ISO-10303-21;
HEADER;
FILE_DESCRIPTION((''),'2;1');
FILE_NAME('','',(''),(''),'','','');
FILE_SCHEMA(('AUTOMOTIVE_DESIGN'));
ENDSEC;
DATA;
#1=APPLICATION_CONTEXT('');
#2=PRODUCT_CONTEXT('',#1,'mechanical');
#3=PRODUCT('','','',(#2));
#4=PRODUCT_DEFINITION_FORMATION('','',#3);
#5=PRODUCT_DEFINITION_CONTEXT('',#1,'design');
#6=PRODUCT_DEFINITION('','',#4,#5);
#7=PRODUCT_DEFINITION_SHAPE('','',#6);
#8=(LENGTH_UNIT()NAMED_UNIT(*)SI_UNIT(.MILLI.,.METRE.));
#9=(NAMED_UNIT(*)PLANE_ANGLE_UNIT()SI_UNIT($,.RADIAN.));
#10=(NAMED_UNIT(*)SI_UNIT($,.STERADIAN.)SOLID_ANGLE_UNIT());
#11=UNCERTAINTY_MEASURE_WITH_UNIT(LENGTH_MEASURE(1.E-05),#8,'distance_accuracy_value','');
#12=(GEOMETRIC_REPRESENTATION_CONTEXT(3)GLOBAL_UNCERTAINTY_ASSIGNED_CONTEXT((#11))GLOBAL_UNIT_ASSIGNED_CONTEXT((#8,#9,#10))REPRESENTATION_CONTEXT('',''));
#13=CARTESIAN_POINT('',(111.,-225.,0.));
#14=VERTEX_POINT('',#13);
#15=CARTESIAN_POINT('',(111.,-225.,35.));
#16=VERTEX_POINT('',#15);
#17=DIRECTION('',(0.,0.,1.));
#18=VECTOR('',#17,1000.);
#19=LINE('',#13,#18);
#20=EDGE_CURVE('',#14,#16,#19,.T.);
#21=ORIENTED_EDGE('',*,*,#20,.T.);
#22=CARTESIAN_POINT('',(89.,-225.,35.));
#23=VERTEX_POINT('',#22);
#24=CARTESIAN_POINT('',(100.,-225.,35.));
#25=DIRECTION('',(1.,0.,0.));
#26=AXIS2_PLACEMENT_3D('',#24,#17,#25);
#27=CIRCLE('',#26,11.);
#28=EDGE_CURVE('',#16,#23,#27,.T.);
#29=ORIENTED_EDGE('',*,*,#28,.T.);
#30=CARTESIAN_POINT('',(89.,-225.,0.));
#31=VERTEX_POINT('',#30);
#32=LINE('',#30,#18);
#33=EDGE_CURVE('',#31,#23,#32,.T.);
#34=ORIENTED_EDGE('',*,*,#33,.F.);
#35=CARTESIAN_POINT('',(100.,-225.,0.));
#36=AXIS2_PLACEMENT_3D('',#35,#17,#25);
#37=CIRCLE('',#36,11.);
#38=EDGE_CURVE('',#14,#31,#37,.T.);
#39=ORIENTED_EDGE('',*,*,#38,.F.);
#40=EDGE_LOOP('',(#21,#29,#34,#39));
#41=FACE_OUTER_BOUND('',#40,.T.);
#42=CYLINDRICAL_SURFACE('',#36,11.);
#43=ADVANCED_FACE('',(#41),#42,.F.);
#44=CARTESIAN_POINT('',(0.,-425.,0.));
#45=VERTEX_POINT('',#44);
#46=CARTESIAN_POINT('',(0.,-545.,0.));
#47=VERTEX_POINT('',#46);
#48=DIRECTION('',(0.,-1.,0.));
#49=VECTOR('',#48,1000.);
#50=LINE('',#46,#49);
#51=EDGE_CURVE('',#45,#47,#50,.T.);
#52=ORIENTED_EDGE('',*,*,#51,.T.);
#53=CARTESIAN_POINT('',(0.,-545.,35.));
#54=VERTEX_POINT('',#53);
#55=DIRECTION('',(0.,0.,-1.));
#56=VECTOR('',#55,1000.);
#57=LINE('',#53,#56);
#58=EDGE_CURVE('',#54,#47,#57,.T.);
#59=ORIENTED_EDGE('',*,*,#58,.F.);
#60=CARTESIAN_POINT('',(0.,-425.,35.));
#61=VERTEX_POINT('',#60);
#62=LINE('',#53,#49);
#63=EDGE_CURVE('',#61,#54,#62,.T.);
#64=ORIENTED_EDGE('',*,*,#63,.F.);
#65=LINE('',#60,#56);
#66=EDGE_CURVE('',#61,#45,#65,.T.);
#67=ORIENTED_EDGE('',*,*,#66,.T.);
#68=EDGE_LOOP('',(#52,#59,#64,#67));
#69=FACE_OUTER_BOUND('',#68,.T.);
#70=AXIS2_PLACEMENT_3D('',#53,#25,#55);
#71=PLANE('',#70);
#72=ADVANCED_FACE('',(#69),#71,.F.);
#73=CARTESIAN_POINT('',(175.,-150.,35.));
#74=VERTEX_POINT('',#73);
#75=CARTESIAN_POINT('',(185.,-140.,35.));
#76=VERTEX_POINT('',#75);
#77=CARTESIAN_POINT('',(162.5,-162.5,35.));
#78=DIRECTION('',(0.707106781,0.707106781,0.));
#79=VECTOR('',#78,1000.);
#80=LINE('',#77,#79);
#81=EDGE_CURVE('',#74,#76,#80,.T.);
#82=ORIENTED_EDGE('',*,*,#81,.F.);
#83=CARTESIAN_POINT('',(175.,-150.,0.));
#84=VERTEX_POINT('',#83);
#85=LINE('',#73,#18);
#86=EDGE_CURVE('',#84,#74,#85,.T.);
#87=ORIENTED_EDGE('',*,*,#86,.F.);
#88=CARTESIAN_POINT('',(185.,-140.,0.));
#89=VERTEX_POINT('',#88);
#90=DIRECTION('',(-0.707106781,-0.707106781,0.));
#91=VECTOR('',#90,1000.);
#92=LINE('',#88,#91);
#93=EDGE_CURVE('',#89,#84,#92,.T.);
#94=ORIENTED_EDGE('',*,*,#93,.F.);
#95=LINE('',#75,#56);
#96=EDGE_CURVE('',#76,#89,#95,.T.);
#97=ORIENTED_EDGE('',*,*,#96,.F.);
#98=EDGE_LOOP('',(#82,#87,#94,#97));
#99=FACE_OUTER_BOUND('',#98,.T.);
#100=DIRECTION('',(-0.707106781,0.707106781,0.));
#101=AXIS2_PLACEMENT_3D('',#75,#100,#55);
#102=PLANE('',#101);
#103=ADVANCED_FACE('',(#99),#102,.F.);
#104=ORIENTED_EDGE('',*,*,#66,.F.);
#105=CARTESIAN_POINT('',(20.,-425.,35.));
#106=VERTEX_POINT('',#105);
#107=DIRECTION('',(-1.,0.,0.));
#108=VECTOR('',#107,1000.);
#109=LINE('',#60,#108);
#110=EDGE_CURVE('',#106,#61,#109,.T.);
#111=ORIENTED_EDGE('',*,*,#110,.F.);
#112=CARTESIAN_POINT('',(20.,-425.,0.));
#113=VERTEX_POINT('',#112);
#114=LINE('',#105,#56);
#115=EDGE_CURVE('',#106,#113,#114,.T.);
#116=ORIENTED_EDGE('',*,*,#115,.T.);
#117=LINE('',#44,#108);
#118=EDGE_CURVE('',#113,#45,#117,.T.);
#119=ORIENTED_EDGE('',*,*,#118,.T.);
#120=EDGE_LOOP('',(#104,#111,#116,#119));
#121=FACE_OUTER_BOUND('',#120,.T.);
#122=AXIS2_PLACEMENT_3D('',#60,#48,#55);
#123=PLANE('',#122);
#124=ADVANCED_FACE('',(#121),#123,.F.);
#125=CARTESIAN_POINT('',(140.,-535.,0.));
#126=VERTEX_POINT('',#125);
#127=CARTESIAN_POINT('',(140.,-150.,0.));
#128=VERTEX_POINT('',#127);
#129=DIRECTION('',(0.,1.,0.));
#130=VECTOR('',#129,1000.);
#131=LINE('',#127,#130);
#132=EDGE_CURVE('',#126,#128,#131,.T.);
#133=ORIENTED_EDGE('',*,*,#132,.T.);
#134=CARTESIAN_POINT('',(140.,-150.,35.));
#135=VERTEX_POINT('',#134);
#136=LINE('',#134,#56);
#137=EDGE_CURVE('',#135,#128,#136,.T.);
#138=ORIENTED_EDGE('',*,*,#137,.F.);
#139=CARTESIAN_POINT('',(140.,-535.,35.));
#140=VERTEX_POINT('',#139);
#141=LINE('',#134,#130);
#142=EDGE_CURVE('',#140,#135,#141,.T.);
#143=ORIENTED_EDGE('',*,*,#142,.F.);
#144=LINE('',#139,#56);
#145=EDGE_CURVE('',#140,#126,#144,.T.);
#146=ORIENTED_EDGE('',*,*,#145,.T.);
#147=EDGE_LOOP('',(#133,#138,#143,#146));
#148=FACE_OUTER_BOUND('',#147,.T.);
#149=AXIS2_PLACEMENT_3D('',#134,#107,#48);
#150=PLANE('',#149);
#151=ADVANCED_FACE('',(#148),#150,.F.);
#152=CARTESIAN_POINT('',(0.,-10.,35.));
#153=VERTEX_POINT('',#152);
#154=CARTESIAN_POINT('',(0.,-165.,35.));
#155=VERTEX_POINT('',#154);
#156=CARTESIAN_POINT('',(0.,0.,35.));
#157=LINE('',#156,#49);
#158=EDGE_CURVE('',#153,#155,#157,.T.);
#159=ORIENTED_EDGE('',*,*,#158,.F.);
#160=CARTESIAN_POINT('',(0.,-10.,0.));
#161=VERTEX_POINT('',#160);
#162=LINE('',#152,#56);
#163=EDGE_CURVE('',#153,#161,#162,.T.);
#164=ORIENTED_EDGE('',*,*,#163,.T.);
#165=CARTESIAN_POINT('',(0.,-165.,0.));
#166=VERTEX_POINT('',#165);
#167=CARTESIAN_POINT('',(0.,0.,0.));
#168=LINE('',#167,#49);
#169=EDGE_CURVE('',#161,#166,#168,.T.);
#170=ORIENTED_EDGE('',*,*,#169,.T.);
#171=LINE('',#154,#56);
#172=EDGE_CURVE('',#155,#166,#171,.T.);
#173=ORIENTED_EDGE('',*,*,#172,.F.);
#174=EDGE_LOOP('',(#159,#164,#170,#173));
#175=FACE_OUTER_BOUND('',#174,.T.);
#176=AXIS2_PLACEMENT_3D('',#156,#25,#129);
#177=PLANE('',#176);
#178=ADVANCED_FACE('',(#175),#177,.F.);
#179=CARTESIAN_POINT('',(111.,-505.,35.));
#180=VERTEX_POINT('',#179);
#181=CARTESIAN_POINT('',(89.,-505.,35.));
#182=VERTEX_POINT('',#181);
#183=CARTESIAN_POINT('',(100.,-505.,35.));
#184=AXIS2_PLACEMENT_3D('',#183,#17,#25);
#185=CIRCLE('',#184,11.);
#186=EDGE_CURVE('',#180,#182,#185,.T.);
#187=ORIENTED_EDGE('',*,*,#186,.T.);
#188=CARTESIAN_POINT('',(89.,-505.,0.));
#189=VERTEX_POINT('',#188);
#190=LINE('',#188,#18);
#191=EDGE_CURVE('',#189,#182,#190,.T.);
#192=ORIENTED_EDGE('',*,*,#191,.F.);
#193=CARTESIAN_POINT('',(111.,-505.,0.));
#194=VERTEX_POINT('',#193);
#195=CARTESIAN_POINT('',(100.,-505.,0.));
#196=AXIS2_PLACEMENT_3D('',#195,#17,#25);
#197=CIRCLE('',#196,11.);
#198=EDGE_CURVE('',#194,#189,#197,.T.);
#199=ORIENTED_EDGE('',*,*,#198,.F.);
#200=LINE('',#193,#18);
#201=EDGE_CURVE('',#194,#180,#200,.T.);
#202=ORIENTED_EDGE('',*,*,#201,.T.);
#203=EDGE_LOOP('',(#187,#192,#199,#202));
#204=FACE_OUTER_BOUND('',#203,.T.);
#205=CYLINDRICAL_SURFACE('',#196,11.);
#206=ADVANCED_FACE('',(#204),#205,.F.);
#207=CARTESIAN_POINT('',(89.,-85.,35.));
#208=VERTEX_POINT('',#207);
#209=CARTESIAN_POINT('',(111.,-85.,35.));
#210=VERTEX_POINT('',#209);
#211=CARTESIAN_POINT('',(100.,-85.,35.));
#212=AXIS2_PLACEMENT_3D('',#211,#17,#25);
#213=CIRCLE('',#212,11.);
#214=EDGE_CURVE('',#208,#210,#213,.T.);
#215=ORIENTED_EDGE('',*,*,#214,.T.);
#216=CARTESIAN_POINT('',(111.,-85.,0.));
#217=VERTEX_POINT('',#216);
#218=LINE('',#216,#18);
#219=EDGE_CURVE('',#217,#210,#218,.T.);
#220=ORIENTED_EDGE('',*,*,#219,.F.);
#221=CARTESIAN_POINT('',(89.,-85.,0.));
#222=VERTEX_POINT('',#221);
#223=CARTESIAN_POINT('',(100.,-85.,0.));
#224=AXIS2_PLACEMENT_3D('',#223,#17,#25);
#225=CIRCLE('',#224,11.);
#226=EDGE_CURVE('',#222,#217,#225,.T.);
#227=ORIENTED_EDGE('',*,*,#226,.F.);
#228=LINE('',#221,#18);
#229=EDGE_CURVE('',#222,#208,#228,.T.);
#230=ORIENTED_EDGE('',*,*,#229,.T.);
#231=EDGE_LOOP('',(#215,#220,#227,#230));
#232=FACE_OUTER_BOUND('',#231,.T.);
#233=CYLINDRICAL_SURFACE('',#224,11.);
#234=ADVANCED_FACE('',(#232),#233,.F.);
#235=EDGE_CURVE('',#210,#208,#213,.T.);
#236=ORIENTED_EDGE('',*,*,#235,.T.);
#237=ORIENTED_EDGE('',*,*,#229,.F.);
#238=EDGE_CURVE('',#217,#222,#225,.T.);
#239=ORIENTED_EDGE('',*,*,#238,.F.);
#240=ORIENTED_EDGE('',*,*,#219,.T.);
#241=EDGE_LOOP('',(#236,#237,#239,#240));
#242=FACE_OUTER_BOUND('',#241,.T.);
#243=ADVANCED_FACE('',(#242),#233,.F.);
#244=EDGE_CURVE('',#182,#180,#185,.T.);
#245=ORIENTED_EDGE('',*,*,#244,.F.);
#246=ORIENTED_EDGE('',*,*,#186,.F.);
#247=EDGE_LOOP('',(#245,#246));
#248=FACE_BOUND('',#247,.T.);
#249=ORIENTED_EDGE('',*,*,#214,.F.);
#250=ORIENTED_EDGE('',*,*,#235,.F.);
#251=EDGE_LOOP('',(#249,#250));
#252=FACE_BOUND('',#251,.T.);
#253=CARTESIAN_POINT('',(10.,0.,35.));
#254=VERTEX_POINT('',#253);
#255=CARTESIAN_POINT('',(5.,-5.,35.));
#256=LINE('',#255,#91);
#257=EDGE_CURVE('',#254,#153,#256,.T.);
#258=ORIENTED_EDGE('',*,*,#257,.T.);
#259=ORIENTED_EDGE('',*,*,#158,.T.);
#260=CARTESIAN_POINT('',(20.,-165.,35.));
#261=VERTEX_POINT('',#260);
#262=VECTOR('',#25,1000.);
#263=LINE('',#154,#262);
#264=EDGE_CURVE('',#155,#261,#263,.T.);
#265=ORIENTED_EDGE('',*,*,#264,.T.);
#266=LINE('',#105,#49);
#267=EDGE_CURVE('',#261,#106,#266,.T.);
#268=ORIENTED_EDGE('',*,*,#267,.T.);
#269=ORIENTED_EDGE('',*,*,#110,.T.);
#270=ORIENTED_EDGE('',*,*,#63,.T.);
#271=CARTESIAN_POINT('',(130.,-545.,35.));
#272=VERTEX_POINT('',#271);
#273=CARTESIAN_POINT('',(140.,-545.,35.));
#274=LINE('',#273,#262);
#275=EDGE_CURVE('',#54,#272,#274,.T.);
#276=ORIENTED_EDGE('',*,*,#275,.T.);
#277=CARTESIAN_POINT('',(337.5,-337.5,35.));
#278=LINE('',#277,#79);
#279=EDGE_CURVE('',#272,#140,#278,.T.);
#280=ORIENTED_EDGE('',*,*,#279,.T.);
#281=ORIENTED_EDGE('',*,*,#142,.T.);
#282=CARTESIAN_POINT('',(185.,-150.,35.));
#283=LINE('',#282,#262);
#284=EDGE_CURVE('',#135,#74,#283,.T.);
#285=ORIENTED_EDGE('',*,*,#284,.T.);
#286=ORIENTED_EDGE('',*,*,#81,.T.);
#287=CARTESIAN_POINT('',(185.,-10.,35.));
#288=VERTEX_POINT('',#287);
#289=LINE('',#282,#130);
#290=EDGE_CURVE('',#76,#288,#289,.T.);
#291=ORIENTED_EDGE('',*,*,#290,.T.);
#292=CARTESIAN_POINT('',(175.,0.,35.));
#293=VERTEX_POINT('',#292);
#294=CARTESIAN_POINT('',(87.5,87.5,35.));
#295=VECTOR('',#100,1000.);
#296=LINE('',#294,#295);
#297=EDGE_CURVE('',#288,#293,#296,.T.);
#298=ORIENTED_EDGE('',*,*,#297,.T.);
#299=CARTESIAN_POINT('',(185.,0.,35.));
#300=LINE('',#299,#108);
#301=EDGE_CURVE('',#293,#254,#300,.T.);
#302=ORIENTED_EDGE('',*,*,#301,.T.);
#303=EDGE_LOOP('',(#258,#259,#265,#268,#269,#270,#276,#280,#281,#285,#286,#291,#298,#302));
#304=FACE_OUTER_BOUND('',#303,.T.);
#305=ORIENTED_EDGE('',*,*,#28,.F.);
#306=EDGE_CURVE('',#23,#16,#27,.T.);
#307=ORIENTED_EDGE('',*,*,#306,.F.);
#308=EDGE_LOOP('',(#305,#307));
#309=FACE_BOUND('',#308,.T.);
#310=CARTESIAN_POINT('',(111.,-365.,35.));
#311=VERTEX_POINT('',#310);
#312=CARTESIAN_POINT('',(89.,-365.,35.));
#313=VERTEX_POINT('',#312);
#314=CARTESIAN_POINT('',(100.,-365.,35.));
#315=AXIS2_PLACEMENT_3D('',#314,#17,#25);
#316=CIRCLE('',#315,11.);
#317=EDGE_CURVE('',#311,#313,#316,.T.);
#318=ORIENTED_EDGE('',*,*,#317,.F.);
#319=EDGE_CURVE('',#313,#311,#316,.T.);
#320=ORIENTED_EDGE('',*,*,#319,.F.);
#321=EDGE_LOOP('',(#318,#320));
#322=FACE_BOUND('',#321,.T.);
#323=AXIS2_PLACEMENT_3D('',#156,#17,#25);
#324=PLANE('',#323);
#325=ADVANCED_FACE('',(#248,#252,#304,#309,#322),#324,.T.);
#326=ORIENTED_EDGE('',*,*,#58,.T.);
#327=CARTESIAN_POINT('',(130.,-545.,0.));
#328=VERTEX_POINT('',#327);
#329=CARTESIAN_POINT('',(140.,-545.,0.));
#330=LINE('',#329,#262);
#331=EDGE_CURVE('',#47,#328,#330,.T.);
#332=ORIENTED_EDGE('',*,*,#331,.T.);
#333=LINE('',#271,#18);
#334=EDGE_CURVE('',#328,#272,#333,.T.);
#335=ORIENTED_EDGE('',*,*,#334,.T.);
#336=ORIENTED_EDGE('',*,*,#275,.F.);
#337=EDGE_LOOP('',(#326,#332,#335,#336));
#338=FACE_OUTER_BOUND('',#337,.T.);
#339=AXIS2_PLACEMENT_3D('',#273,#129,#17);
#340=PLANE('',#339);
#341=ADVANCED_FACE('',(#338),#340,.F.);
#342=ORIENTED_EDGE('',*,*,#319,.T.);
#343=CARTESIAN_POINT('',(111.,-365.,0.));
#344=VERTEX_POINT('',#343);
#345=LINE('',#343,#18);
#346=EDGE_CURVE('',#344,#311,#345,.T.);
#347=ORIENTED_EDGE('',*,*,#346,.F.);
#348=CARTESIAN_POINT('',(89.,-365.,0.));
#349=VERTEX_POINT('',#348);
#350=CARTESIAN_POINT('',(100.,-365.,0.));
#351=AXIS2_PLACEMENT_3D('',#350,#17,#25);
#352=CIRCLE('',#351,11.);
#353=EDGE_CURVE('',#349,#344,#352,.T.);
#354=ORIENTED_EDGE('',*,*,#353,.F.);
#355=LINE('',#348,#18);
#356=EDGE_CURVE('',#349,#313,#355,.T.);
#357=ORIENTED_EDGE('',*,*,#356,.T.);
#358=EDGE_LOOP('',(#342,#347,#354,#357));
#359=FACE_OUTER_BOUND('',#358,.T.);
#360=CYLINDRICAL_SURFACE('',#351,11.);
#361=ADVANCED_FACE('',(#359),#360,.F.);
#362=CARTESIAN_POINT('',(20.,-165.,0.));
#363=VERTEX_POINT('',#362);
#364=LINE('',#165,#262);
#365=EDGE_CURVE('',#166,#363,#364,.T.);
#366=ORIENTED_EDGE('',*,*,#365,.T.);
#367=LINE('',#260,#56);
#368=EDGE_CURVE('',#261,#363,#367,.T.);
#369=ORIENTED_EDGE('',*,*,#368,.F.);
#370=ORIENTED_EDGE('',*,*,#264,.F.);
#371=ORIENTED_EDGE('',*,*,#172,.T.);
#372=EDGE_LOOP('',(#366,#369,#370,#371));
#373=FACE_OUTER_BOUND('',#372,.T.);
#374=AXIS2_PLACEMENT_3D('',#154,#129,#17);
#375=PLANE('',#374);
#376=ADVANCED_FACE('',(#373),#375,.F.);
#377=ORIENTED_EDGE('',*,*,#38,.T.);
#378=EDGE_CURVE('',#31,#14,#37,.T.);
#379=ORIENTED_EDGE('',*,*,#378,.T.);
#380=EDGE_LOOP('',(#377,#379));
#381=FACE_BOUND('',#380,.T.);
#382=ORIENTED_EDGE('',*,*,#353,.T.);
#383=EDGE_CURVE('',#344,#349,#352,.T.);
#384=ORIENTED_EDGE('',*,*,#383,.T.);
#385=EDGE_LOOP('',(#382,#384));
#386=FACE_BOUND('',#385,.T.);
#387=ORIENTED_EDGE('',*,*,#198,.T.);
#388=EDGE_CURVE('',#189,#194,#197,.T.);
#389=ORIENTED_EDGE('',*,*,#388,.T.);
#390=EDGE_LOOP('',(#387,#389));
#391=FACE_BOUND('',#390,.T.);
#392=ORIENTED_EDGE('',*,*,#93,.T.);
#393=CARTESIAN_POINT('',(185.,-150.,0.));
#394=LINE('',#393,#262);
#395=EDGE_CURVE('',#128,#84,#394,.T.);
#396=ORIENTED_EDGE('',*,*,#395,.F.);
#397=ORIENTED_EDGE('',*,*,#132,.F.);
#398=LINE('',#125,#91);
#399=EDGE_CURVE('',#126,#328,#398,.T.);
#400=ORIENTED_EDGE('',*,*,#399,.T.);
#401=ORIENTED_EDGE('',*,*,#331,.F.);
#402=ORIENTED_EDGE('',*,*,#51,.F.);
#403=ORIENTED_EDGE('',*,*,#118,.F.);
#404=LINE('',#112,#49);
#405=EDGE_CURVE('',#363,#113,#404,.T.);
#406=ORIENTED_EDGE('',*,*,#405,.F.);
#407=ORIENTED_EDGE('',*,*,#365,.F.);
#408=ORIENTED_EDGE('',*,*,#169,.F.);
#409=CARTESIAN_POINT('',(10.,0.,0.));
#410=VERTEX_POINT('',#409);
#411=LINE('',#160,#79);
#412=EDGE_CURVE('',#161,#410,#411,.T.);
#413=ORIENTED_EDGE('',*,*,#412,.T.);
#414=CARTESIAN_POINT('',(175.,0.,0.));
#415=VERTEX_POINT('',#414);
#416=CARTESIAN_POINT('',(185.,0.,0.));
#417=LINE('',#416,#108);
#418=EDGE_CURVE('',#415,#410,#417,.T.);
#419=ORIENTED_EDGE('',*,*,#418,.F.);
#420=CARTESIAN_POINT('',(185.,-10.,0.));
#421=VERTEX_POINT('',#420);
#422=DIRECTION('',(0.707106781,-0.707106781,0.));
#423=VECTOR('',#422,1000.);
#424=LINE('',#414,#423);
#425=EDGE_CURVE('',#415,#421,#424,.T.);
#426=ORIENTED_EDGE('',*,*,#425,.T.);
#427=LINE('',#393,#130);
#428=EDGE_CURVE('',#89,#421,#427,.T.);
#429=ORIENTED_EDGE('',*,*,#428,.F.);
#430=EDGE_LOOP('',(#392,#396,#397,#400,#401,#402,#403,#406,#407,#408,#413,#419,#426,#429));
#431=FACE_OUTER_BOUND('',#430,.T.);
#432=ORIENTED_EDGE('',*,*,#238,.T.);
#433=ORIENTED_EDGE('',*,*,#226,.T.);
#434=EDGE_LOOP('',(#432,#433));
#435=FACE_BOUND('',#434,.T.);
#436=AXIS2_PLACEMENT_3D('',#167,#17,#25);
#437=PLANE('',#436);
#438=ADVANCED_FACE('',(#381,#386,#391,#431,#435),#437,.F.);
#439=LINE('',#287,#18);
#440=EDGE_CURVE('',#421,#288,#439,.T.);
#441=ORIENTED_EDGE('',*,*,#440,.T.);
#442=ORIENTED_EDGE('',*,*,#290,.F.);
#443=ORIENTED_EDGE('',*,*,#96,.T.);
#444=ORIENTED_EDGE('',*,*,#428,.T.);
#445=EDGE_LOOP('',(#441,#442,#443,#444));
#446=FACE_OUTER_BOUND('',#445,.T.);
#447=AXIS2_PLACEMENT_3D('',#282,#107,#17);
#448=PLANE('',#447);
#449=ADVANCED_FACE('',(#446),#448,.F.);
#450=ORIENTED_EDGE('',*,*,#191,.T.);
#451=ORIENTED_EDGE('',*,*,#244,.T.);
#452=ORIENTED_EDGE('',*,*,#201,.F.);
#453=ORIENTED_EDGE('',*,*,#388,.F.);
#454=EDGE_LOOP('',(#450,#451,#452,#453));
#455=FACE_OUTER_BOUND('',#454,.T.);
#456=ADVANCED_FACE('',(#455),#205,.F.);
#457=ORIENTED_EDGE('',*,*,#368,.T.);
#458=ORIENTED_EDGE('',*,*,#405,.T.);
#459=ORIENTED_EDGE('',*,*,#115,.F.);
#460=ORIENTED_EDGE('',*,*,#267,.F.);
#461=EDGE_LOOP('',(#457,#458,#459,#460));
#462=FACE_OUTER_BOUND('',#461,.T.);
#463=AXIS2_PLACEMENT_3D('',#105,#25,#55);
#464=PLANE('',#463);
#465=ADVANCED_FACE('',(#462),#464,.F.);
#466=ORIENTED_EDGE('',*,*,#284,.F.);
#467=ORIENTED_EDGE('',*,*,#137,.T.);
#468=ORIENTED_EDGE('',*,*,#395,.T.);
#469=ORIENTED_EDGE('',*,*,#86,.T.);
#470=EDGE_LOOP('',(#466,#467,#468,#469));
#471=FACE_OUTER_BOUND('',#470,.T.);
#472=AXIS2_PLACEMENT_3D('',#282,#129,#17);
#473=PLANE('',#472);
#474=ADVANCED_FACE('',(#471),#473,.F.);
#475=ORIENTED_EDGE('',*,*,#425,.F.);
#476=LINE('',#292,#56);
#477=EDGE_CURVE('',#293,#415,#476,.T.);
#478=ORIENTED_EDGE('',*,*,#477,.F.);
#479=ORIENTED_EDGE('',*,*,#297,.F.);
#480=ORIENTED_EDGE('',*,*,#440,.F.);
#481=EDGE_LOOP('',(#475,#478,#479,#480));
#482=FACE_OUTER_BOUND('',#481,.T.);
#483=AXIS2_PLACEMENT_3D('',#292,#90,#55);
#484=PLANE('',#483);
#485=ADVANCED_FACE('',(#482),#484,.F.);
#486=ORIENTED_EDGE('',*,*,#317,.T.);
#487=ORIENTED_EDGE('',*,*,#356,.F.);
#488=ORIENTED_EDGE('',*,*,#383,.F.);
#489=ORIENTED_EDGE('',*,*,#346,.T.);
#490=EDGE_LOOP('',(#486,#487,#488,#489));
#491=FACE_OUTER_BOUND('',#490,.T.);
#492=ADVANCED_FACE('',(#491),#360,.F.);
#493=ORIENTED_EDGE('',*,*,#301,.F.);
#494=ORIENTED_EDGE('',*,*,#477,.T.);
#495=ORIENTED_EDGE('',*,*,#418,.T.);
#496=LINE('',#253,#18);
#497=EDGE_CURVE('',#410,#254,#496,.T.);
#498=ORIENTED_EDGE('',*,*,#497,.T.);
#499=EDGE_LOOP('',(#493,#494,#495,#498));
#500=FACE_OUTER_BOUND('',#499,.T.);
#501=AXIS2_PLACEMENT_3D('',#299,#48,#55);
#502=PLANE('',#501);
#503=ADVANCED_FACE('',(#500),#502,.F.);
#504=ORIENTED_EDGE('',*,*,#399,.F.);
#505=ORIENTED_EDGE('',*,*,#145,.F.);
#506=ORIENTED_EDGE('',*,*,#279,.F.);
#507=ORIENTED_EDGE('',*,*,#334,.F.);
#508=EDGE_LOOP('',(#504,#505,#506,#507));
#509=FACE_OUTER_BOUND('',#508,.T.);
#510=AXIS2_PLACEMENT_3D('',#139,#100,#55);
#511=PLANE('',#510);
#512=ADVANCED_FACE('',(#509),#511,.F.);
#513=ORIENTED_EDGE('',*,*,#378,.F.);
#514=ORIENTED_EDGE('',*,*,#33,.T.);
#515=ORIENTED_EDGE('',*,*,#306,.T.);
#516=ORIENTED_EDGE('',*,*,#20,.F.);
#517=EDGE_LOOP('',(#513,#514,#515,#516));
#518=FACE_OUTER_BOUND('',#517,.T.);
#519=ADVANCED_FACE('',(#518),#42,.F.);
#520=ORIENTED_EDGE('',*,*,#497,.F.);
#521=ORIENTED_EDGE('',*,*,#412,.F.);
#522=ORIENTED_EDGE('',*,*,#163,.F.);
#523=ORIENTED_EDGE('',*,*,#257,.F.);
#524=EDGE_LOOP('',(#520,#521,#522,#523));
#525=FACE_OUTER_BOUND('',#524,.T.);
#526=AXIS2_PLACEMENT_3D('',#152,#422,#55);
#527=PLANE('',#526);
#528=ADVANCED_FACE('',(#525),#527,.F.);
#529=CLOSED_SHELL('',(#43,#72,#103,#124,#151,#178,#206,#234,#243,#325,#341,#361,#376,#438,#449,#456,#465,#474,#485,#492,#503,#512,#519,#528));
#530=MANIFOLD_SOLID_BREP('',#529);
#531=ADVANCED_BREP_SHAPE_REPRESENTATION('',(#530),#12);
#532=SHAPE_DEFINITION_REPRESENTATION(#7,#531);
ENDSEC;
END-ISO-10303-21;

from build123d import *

# Parameters (mm, degrees)
BOSS_EXTRUDE1_DEPTH     = 35
CHAMFER1_SIZE           = 10
CUT_EXTRUDE1_DEPTH      = 577.606451577
CUT_EXTRUDE1_DEPTH_BACK = 577.606451577
SKETCH2_R               = 11


with BuildPart() as part:
    # Sketch1 → Boss-Extrude1 (new body)
    with BuildSketch(Plane.XY):
        Polygon((185, -150), (185, 0), (0, 0), (0, -165), (20, -165), (20, -425), (0, -425), (0, -545), (140, -545), (140, -150), align=None)
    extrude(amount=BOSS_EXTRUDE1_DEPTH)

    # Chamfer1
    chamfer1_edges = [part.edges().sort_by_distance(p)[0] for p in [
        (140, -545, 17.5),
        (0, 0, 17.5),
        (185, 0, 17.5),
        (185, -150, 17.5),
    ]]
    chamfer(chamfer1_edges, length=CHAMFER1_SIZE)

    # Sketch2 → Cut-Extrude1 (cut, two sides: drawn at the far end of the back side and taken through both)
    with BuildSketch(Plane.XY.offset(35).offset(-CUT_EXTRUDE1_DEPTH_BACK)):
        with Locations((100, -85)):
            Circle(SKETCH2_R)
        with Locations((100, -225)):
            Circle(SKETCH2_R)
        with Locations((100, -365)):
            Circle(SKETCH2_R)
        with Locations((100, -505)):
            Circle(SKETCH2_R)
    extrude(amount=CUT_EXTRUDE1_DEPTH + CUT_EXTRUDE1_DEPTH_BACK, mode=Mode.SUBTRACT)


solid = part.part
